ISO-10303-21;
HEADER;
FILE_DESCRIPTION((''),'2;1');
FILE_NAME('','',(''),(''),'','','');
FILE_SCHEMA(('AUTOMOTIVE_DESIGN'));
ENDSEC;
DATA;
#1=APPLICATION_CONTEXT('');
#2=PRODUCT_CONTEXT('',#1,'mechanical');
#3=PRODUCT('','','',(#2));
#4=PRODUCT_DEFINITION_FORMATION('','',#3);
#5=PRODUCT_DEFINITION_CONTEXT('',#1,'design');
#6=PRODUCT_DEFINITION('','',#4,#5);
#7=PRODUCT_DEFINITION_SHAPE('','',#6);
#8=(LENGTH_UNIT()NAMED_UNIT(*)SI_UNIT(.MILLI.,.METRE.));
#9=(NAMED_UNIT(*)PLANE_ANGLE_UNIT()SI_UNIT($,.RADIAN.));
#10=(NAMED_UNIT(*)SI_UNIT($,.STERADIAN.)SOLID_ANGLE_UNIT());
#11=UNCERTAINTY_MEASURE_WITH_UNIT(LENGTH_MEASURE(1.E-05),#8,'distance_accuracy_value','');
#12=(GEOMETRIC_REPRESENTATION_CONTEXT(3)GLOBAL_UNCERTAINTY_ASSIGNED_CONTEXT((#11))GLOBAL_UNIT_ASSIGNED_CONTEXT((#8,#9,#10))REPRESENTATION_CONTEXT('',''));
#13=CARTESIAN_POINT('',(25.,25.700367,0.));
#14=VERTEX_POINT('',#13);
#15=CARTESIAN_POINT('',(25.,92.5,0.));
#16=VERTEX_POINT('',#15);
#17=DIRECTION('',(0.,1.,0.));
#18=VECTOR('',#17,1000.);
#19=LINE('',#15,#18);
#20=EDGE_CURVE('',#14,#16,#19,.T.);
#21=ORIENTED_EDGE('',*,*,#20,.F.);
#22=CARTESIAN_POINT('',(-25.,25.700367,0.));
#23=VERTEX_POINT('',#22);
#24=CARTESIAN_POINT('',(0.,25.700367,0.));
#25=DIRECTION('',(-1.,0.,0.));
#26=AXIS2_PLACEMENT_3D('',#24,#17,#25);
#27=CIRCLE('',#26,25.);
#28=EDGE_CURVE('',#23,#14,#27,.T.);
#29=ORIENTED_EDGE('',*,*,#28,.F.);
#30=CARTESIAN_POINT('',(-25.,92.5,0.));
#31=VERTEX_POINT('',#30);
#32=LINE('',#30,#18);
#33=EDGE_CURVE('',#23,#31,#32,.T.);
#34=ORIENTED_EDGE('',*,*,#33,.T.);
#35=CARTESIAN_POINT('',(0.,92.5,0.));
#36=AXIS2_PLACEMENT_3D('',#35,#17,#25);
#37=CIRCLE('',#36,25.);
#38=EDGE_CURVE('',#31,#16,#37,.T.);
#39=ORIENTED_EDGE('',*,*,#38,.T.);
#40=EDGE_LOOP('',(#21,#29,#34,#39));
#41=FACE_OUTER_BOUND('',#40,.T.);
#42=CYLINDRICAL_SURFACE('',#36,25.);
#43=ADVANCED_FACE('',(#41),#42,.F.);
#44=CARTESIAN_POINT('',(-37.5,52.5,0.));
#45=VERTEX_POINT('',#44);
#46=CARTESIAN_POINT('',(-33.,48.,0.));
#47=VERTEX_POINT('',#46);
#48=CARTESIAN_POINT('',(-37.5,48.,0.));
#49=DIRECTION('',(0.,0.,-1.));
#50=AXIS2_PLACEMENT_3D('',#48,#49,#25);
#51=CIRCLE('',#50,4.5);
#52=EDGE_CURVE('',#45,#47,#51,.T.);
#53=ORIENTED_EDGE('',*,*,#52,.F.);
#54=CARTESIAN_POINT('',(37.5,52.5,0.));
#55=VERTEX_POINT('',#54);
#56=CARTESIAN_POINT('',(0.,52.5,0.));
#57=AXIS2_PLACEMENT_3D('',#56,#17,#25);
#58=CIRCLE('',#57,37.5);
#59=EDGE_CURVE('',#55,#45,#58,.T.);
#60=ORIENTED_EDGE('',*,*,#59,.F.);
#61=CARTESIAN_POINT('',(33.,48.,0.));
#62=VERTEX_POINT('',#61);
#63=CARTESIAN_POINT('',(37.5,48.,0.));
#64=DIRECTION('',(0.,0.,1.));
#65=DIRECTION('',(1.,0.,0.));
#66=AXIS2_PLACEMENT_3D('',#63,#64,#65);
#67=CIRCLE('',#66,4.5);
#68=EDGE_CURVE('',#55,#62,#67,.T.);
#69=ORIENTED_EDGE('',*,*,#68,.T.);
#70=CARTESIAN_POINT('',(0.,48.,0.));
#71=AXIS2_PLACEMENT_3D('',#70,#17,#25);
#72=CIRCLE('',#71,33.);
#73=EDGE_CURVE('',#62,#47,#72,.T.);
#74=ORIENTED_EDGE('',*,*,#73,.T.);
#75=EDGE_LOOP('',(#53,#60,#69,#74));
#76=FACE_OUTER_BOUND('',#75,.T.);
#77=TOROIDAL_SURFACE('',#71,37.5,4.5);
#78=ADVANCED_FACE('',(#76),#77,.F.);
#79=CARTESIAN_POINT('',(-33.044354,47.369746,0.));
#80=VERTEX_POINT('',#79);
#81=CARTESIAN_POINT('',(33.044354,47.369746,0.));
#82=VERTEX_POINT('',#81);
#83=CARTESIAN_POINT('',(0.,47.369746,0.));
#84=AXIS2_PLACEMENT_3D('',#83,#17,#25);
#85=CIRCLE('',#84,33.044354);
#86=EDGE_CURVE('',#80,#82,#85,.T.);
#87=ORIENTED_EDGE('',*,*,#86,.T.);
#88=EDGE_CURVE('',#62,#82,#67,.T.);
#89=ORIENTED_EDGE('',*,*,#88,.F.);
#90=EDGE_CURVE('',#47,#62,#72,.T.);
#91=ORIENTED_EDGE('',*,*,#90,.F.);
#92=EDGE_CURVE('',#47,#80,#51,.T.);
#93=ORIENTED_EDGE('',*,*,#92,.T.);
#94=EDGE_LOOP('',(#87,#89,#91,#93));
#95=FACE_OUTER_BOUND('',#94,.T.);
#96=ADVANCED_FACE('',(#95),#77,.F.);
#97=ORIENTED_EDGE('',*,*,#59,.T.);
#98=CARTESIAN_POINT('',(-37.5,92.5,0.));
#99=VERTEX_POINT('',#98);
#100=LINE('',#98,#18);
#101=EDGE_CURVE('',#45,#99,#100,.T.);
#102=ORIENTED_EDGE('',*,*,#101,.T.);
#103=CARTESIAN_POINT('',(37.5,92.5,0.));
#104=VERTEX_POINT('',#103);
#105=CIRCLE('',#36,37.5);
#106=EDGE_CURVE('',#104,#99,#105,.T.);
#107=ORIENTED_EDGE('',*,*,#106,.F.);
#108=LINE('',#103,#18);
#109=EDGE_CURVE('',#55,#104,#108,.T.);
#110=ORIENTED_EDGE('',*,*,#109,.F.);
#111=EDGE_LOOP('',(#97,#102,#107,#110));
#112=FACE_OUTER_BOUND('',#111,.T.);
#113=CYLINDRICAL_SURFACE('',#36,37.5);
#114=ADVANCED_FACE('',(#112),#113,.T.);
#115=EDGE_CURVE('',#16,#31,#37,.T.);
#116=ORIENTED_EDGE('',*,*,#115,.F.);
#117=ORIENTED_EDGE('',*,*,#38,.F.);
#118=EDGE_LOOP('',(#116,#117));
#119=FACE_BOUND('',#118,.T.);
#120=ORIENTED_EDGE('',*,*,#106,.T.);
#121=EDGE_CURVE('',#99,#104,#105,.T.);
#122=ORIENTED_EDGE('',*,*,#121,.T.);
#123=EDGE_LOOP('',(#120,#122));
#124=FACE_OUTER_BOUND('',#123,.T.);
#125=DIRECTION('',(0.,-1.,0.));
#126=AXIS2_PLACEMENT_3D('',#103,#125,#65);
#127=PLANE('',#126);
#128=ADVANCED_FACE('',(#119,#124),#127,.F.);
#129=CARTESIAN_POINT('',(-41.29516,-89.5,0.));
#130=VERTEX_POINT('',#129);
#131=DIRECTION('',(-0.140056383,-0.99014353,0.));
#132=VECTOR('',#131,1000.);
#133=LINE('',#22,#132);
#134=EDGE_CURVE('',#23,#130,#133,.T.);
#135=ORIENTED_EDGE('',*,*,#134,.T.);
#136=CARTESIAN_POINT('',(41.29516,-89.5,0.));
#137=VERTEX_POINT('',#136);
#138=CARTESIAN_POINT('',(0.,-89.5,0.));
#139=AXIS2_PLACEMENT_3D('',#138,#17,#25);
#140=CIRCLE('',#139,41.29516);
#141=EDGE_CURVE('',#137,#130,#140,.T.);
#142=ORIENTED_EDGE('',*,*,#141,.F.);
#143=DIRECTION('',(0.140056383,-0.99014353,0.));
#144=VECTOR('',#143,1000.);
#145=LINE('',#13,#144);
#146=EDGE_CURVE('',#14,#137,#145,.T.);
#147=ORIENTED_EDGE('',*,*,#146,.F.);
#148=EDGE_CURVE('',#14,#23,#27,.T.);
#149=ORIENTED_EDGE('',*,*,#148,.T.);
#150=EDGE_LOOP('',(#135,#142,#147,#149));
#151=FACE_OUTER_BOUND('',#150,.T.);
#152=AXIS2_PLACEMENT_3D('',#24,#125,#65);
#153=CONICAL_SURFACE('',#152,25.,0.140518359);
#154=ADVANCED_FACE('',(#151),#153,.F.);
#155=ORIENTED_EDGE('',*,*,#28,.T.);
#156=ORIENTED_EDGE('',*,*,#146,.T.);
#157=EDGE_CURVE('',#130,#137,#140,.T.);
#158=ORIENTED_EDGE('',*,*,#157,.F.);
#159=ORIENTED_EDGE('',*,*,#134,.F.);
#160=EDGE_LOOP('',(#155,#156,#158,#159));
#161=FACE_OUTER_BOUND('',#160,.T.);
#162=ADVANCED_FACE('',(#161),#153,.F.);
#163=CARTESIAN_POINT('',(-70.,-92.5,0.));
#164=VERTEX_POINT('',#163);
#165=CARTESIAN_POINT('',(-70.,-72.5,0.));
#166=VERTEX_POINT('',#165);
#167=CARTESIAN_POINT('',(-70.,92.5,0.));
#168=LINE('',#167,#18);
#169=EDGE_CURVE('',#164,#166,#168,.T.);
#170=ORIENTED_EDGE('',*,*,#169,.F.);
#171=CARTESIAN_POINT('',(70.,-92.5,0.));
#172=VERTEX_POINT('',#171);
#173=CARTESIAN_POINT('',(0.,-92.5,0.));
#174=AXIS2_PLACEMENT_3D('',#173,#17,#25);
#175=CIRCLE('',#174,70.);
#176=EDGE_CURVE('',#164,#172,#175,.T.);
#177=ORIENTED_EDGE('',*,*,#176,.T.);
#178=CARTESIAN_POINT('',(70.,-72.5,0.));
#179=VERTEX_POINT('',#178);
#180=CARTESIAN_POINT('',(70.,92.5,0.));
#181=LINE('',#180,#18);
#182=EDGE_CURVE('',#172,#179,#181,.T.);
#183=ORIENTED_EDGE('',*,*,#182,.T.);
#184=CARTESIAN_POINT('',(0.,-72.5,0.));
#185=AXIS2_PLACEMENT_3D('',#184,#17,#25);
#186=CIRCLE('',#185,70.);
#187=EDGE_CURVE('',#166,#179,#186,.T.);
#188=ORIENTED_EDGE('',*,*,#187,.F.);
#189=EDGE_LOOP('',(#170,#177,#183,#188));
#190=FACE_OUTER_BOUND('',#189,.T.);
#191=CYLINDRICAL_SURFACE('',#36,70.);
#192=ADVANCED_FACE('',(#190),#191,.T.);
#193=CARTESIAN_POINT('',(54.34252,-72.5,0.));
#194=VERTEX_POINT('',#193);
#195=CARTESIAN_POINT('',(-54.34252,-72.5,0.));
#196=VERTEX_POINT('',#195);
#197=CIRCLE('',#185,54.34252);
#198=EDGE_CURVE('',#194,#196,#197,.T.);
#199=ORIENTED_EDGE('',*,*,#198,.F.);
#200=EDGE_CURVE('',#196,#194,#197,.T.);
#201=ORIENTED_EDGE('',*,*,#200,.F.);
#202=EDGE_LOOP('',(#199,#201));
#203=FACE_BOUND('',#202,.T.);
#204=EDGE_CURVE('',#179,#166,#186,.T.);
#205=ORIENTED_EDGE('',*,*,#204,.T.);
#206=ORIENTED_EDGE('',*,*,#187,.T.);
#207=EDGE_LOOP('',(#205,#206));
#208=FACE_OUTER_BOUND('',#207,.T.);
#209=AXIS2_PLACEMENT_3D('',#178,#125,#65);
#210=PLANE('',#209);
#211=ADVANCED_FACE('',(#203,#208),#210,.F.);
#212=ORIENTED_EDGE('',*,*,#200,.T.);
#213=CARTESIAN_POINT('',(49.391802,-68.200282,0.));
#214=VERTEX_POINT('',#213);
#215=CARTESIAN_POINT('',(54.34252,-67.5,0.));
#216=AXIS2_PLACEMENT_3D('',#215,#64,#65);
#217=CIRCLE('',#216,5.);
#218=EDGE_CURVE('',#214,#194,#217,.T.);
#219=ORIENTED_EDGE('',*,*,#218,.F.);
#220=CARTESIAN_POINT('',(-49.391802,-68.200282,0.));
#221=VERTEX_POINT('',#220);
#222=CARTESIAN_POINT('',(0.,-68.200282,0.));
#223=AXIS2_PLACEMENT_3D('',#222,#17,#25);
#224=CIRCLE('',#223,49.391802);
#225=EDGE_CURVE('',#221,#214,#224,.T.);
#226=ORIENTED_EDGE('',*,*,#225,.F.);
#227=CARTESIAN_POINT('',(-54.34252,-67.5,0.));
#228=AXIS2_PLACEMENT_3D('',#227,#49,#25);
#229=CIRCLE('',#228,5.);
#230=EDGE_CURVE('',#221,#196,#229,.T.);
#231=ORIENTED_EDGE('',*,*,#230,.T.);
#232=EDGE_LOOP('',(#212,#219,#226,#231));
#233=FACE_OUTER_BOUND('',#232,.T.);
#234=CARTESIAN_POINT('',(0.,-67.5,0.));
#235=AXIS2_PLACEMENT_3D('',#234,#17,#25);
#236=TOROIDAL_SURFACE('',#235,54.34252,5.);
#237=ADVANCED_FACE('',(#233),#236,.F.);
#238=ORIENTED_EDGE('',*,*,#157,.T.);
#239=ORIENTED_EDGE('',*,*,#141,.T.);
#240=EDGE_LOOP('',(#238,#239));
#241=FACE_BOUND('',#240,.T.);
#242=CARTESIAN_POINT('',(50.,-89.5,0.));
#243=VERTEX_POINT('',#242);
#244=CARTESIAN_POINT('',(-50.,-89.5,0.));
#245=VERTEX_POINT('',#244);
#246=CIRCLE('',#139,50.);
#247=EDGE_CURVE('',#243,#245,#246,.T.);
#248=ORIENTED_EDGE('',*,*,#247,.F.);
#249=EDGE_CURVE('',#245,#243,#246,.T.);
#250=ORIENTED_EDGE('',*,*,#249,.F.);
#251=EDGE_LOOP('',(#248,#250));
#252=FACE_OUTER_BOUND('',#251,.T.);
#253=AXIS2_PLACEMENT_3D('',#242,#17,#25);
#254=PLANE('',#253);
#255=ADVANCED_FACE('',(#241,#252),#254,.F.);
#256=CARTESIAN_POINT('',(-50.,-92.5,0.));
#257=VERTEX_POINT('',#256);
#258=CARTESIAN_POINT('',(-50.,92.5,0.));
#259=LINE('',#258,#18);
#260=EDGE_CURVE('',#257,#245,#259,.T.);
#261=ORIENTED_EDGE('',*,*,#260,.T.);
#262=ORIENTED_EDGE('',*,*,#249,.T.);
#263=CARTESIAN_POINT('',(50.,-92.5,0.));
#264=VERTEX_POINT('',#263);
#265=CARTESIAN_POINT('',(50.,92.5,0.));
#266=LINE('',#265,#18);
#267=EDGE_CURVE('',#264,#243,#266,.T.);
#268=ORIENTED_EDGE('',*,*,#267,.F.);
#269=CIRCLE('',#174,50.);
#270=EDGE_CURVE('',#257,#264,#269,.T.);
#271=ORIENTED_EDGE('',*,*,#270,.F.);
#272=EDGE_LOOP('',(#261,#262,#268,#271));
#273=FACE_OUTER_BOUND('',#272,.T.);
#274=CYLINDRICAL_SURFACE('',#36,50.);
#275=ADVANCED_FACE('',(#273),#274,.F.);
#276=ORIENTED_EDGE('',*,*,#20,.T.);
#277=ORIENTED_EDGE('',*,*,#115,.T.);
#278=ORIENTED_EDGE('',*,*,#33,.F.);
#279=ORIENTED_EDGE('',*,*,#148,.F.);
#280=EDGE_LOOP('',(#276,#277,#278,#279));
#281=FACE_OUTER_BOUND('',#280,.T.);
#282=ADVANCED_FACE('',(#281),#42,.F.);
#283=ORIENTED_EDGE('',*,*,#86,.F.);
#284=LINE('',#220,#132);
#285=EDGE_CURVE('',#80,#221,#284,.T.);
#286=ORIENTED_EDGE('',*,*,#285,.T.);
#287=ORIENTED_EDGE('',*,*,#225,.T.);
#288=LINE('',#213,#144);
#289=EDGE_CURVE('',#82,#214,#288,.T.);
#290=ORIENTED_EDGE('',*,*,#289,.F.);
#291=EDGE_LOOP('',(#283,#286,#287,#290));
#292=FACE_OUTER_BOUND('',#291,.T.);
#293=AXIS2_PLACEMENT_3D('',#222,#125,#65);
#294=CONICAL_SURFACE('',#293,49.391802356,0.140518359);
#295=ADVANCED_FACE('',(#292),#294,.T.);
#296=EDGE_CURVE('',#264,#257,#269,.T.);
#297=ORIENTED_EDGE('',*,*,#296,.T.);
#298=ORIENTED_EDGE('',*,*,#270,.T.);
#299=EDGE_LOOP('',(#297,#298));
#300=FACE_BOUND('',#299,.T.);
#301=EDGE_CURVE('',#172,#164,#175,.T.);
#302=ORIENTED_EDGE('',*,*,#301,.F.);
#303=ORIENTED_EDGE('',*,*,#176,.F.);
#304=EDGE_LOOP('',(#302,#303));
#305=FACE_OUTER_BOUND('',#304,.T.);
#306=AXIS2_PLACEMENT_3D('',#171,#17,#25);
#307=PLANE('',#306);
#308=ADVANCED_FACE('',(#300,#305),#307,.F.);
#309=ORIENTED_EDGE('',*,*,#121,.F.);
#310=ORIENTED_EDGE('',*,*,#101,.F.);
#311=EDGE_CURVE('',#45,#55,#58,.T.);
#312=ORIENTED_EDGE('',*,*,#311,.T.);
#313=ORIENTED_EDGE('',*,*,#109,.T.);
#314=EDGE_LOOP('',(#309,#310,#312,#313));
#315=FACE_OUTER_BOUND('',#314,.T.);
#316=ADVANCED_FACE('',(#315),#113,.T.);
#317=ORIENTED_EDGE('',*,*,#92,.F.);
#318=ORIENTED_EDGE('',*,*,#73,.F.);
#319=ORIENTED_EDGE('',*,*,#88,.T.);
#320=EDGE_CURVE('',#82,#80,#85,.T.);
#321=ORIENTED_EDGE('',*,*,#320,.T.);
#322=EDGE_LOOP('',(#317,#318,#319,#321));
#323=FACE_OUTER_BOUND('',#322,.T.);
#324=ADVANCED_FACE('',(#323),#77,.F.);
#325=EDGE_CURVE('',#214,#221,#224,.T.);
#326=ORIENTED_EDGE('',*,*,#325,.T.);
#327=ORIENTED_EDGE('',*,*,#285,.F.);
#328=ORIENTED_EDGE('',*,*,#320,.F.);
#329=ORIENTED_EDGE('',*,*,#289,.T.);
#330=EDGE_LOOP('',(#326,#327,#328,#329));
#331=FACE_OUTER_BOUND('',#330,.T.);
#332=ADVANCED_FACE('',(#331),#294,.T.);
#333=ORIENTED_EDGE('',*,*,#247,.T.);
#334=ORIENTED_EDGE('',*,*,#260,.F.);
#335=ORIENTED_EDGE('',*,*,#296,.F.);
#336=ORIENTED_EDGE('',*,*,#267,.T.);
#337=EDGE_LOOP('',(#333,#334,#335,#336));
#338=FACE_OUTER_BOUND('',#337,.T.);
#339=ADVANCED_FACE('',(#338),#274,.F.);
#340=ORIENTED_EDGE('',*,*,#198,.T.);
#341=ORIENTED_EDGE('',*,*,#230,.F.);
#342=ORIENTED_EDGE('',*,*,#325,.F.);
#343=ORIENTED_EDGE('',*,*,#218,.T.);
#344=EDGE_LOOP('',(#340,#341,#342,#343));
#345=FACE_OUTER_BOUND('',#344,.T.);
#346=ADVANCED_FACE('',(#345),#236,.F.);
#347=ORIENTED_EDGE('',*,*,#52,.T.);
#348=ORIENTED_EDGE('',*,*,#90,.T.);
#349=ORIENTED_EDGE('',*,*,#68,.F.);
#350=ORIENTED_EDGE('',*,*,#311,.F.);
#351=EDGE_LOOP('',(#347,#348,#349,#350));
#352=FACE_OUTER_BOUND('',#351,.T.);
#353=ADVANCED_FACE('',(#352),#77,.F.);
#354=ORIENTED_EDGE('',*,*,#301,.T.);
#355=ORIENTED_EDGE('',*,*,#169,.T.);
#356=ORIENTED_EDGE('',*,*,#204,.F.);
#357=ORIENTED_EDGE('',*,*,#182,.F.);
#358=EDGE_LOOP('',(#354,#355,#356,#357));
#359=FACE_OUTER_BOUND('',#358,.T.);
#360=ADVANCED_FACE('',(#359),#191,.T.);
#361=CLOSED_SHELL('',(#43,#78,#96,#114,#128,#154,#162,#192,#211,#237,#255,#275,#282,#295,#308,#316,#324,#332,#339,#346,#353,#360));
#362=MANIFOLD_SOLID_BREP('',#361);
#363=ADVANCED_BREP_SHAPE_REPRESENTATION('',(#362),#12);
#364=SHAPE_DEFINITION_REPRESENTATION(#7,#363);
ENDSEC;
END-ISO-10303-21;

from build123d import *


with BuildPart() as part:
    # Sketch1 → Revolve1 (revolve)
    with BuildSketch(Plane.XY, mode=Mode.PRIVATE) as revolve1_sk:
        with BuildLine():
            Line((37.5, 92.5), (25, 92.5))
            Line((25, 92.5), (25, 25.700367412))
            Line((25, 25.700367412), (41.295159506, -89.5))
            Line((41.295159506, -89.5), (50, -89.5))
            Line((50, -89.5), (50, -92.5))
            Line((50, -92.5), (70, -92.5))
            Line((70, -92.5), (70, -72.5))
            Line((70, -72.5), (54.342520005, -72.5))
            ThreePointArc((54.342520005, -72.5), (51.063908223, -71.275010567), (49.391802356, -68.200281914))
            Line((49.391802356, -68.200281914), (33.044354116, 47.369746278))
            ThreePointArc((33.044354116, 47.369746278), (34.102490489, 50.950750604), (37.5, 52.5))
            Line((37.5, 52.5), (37.5, 92.5))
        make_face()
    revolve(revolve1_sk.sketch.rotate(Axis((0, 92.5, 0), (0, -1, 0)), 180), axis=Axis((0, 92.5, 0), (0, -1, 0)))


solid = part.part
